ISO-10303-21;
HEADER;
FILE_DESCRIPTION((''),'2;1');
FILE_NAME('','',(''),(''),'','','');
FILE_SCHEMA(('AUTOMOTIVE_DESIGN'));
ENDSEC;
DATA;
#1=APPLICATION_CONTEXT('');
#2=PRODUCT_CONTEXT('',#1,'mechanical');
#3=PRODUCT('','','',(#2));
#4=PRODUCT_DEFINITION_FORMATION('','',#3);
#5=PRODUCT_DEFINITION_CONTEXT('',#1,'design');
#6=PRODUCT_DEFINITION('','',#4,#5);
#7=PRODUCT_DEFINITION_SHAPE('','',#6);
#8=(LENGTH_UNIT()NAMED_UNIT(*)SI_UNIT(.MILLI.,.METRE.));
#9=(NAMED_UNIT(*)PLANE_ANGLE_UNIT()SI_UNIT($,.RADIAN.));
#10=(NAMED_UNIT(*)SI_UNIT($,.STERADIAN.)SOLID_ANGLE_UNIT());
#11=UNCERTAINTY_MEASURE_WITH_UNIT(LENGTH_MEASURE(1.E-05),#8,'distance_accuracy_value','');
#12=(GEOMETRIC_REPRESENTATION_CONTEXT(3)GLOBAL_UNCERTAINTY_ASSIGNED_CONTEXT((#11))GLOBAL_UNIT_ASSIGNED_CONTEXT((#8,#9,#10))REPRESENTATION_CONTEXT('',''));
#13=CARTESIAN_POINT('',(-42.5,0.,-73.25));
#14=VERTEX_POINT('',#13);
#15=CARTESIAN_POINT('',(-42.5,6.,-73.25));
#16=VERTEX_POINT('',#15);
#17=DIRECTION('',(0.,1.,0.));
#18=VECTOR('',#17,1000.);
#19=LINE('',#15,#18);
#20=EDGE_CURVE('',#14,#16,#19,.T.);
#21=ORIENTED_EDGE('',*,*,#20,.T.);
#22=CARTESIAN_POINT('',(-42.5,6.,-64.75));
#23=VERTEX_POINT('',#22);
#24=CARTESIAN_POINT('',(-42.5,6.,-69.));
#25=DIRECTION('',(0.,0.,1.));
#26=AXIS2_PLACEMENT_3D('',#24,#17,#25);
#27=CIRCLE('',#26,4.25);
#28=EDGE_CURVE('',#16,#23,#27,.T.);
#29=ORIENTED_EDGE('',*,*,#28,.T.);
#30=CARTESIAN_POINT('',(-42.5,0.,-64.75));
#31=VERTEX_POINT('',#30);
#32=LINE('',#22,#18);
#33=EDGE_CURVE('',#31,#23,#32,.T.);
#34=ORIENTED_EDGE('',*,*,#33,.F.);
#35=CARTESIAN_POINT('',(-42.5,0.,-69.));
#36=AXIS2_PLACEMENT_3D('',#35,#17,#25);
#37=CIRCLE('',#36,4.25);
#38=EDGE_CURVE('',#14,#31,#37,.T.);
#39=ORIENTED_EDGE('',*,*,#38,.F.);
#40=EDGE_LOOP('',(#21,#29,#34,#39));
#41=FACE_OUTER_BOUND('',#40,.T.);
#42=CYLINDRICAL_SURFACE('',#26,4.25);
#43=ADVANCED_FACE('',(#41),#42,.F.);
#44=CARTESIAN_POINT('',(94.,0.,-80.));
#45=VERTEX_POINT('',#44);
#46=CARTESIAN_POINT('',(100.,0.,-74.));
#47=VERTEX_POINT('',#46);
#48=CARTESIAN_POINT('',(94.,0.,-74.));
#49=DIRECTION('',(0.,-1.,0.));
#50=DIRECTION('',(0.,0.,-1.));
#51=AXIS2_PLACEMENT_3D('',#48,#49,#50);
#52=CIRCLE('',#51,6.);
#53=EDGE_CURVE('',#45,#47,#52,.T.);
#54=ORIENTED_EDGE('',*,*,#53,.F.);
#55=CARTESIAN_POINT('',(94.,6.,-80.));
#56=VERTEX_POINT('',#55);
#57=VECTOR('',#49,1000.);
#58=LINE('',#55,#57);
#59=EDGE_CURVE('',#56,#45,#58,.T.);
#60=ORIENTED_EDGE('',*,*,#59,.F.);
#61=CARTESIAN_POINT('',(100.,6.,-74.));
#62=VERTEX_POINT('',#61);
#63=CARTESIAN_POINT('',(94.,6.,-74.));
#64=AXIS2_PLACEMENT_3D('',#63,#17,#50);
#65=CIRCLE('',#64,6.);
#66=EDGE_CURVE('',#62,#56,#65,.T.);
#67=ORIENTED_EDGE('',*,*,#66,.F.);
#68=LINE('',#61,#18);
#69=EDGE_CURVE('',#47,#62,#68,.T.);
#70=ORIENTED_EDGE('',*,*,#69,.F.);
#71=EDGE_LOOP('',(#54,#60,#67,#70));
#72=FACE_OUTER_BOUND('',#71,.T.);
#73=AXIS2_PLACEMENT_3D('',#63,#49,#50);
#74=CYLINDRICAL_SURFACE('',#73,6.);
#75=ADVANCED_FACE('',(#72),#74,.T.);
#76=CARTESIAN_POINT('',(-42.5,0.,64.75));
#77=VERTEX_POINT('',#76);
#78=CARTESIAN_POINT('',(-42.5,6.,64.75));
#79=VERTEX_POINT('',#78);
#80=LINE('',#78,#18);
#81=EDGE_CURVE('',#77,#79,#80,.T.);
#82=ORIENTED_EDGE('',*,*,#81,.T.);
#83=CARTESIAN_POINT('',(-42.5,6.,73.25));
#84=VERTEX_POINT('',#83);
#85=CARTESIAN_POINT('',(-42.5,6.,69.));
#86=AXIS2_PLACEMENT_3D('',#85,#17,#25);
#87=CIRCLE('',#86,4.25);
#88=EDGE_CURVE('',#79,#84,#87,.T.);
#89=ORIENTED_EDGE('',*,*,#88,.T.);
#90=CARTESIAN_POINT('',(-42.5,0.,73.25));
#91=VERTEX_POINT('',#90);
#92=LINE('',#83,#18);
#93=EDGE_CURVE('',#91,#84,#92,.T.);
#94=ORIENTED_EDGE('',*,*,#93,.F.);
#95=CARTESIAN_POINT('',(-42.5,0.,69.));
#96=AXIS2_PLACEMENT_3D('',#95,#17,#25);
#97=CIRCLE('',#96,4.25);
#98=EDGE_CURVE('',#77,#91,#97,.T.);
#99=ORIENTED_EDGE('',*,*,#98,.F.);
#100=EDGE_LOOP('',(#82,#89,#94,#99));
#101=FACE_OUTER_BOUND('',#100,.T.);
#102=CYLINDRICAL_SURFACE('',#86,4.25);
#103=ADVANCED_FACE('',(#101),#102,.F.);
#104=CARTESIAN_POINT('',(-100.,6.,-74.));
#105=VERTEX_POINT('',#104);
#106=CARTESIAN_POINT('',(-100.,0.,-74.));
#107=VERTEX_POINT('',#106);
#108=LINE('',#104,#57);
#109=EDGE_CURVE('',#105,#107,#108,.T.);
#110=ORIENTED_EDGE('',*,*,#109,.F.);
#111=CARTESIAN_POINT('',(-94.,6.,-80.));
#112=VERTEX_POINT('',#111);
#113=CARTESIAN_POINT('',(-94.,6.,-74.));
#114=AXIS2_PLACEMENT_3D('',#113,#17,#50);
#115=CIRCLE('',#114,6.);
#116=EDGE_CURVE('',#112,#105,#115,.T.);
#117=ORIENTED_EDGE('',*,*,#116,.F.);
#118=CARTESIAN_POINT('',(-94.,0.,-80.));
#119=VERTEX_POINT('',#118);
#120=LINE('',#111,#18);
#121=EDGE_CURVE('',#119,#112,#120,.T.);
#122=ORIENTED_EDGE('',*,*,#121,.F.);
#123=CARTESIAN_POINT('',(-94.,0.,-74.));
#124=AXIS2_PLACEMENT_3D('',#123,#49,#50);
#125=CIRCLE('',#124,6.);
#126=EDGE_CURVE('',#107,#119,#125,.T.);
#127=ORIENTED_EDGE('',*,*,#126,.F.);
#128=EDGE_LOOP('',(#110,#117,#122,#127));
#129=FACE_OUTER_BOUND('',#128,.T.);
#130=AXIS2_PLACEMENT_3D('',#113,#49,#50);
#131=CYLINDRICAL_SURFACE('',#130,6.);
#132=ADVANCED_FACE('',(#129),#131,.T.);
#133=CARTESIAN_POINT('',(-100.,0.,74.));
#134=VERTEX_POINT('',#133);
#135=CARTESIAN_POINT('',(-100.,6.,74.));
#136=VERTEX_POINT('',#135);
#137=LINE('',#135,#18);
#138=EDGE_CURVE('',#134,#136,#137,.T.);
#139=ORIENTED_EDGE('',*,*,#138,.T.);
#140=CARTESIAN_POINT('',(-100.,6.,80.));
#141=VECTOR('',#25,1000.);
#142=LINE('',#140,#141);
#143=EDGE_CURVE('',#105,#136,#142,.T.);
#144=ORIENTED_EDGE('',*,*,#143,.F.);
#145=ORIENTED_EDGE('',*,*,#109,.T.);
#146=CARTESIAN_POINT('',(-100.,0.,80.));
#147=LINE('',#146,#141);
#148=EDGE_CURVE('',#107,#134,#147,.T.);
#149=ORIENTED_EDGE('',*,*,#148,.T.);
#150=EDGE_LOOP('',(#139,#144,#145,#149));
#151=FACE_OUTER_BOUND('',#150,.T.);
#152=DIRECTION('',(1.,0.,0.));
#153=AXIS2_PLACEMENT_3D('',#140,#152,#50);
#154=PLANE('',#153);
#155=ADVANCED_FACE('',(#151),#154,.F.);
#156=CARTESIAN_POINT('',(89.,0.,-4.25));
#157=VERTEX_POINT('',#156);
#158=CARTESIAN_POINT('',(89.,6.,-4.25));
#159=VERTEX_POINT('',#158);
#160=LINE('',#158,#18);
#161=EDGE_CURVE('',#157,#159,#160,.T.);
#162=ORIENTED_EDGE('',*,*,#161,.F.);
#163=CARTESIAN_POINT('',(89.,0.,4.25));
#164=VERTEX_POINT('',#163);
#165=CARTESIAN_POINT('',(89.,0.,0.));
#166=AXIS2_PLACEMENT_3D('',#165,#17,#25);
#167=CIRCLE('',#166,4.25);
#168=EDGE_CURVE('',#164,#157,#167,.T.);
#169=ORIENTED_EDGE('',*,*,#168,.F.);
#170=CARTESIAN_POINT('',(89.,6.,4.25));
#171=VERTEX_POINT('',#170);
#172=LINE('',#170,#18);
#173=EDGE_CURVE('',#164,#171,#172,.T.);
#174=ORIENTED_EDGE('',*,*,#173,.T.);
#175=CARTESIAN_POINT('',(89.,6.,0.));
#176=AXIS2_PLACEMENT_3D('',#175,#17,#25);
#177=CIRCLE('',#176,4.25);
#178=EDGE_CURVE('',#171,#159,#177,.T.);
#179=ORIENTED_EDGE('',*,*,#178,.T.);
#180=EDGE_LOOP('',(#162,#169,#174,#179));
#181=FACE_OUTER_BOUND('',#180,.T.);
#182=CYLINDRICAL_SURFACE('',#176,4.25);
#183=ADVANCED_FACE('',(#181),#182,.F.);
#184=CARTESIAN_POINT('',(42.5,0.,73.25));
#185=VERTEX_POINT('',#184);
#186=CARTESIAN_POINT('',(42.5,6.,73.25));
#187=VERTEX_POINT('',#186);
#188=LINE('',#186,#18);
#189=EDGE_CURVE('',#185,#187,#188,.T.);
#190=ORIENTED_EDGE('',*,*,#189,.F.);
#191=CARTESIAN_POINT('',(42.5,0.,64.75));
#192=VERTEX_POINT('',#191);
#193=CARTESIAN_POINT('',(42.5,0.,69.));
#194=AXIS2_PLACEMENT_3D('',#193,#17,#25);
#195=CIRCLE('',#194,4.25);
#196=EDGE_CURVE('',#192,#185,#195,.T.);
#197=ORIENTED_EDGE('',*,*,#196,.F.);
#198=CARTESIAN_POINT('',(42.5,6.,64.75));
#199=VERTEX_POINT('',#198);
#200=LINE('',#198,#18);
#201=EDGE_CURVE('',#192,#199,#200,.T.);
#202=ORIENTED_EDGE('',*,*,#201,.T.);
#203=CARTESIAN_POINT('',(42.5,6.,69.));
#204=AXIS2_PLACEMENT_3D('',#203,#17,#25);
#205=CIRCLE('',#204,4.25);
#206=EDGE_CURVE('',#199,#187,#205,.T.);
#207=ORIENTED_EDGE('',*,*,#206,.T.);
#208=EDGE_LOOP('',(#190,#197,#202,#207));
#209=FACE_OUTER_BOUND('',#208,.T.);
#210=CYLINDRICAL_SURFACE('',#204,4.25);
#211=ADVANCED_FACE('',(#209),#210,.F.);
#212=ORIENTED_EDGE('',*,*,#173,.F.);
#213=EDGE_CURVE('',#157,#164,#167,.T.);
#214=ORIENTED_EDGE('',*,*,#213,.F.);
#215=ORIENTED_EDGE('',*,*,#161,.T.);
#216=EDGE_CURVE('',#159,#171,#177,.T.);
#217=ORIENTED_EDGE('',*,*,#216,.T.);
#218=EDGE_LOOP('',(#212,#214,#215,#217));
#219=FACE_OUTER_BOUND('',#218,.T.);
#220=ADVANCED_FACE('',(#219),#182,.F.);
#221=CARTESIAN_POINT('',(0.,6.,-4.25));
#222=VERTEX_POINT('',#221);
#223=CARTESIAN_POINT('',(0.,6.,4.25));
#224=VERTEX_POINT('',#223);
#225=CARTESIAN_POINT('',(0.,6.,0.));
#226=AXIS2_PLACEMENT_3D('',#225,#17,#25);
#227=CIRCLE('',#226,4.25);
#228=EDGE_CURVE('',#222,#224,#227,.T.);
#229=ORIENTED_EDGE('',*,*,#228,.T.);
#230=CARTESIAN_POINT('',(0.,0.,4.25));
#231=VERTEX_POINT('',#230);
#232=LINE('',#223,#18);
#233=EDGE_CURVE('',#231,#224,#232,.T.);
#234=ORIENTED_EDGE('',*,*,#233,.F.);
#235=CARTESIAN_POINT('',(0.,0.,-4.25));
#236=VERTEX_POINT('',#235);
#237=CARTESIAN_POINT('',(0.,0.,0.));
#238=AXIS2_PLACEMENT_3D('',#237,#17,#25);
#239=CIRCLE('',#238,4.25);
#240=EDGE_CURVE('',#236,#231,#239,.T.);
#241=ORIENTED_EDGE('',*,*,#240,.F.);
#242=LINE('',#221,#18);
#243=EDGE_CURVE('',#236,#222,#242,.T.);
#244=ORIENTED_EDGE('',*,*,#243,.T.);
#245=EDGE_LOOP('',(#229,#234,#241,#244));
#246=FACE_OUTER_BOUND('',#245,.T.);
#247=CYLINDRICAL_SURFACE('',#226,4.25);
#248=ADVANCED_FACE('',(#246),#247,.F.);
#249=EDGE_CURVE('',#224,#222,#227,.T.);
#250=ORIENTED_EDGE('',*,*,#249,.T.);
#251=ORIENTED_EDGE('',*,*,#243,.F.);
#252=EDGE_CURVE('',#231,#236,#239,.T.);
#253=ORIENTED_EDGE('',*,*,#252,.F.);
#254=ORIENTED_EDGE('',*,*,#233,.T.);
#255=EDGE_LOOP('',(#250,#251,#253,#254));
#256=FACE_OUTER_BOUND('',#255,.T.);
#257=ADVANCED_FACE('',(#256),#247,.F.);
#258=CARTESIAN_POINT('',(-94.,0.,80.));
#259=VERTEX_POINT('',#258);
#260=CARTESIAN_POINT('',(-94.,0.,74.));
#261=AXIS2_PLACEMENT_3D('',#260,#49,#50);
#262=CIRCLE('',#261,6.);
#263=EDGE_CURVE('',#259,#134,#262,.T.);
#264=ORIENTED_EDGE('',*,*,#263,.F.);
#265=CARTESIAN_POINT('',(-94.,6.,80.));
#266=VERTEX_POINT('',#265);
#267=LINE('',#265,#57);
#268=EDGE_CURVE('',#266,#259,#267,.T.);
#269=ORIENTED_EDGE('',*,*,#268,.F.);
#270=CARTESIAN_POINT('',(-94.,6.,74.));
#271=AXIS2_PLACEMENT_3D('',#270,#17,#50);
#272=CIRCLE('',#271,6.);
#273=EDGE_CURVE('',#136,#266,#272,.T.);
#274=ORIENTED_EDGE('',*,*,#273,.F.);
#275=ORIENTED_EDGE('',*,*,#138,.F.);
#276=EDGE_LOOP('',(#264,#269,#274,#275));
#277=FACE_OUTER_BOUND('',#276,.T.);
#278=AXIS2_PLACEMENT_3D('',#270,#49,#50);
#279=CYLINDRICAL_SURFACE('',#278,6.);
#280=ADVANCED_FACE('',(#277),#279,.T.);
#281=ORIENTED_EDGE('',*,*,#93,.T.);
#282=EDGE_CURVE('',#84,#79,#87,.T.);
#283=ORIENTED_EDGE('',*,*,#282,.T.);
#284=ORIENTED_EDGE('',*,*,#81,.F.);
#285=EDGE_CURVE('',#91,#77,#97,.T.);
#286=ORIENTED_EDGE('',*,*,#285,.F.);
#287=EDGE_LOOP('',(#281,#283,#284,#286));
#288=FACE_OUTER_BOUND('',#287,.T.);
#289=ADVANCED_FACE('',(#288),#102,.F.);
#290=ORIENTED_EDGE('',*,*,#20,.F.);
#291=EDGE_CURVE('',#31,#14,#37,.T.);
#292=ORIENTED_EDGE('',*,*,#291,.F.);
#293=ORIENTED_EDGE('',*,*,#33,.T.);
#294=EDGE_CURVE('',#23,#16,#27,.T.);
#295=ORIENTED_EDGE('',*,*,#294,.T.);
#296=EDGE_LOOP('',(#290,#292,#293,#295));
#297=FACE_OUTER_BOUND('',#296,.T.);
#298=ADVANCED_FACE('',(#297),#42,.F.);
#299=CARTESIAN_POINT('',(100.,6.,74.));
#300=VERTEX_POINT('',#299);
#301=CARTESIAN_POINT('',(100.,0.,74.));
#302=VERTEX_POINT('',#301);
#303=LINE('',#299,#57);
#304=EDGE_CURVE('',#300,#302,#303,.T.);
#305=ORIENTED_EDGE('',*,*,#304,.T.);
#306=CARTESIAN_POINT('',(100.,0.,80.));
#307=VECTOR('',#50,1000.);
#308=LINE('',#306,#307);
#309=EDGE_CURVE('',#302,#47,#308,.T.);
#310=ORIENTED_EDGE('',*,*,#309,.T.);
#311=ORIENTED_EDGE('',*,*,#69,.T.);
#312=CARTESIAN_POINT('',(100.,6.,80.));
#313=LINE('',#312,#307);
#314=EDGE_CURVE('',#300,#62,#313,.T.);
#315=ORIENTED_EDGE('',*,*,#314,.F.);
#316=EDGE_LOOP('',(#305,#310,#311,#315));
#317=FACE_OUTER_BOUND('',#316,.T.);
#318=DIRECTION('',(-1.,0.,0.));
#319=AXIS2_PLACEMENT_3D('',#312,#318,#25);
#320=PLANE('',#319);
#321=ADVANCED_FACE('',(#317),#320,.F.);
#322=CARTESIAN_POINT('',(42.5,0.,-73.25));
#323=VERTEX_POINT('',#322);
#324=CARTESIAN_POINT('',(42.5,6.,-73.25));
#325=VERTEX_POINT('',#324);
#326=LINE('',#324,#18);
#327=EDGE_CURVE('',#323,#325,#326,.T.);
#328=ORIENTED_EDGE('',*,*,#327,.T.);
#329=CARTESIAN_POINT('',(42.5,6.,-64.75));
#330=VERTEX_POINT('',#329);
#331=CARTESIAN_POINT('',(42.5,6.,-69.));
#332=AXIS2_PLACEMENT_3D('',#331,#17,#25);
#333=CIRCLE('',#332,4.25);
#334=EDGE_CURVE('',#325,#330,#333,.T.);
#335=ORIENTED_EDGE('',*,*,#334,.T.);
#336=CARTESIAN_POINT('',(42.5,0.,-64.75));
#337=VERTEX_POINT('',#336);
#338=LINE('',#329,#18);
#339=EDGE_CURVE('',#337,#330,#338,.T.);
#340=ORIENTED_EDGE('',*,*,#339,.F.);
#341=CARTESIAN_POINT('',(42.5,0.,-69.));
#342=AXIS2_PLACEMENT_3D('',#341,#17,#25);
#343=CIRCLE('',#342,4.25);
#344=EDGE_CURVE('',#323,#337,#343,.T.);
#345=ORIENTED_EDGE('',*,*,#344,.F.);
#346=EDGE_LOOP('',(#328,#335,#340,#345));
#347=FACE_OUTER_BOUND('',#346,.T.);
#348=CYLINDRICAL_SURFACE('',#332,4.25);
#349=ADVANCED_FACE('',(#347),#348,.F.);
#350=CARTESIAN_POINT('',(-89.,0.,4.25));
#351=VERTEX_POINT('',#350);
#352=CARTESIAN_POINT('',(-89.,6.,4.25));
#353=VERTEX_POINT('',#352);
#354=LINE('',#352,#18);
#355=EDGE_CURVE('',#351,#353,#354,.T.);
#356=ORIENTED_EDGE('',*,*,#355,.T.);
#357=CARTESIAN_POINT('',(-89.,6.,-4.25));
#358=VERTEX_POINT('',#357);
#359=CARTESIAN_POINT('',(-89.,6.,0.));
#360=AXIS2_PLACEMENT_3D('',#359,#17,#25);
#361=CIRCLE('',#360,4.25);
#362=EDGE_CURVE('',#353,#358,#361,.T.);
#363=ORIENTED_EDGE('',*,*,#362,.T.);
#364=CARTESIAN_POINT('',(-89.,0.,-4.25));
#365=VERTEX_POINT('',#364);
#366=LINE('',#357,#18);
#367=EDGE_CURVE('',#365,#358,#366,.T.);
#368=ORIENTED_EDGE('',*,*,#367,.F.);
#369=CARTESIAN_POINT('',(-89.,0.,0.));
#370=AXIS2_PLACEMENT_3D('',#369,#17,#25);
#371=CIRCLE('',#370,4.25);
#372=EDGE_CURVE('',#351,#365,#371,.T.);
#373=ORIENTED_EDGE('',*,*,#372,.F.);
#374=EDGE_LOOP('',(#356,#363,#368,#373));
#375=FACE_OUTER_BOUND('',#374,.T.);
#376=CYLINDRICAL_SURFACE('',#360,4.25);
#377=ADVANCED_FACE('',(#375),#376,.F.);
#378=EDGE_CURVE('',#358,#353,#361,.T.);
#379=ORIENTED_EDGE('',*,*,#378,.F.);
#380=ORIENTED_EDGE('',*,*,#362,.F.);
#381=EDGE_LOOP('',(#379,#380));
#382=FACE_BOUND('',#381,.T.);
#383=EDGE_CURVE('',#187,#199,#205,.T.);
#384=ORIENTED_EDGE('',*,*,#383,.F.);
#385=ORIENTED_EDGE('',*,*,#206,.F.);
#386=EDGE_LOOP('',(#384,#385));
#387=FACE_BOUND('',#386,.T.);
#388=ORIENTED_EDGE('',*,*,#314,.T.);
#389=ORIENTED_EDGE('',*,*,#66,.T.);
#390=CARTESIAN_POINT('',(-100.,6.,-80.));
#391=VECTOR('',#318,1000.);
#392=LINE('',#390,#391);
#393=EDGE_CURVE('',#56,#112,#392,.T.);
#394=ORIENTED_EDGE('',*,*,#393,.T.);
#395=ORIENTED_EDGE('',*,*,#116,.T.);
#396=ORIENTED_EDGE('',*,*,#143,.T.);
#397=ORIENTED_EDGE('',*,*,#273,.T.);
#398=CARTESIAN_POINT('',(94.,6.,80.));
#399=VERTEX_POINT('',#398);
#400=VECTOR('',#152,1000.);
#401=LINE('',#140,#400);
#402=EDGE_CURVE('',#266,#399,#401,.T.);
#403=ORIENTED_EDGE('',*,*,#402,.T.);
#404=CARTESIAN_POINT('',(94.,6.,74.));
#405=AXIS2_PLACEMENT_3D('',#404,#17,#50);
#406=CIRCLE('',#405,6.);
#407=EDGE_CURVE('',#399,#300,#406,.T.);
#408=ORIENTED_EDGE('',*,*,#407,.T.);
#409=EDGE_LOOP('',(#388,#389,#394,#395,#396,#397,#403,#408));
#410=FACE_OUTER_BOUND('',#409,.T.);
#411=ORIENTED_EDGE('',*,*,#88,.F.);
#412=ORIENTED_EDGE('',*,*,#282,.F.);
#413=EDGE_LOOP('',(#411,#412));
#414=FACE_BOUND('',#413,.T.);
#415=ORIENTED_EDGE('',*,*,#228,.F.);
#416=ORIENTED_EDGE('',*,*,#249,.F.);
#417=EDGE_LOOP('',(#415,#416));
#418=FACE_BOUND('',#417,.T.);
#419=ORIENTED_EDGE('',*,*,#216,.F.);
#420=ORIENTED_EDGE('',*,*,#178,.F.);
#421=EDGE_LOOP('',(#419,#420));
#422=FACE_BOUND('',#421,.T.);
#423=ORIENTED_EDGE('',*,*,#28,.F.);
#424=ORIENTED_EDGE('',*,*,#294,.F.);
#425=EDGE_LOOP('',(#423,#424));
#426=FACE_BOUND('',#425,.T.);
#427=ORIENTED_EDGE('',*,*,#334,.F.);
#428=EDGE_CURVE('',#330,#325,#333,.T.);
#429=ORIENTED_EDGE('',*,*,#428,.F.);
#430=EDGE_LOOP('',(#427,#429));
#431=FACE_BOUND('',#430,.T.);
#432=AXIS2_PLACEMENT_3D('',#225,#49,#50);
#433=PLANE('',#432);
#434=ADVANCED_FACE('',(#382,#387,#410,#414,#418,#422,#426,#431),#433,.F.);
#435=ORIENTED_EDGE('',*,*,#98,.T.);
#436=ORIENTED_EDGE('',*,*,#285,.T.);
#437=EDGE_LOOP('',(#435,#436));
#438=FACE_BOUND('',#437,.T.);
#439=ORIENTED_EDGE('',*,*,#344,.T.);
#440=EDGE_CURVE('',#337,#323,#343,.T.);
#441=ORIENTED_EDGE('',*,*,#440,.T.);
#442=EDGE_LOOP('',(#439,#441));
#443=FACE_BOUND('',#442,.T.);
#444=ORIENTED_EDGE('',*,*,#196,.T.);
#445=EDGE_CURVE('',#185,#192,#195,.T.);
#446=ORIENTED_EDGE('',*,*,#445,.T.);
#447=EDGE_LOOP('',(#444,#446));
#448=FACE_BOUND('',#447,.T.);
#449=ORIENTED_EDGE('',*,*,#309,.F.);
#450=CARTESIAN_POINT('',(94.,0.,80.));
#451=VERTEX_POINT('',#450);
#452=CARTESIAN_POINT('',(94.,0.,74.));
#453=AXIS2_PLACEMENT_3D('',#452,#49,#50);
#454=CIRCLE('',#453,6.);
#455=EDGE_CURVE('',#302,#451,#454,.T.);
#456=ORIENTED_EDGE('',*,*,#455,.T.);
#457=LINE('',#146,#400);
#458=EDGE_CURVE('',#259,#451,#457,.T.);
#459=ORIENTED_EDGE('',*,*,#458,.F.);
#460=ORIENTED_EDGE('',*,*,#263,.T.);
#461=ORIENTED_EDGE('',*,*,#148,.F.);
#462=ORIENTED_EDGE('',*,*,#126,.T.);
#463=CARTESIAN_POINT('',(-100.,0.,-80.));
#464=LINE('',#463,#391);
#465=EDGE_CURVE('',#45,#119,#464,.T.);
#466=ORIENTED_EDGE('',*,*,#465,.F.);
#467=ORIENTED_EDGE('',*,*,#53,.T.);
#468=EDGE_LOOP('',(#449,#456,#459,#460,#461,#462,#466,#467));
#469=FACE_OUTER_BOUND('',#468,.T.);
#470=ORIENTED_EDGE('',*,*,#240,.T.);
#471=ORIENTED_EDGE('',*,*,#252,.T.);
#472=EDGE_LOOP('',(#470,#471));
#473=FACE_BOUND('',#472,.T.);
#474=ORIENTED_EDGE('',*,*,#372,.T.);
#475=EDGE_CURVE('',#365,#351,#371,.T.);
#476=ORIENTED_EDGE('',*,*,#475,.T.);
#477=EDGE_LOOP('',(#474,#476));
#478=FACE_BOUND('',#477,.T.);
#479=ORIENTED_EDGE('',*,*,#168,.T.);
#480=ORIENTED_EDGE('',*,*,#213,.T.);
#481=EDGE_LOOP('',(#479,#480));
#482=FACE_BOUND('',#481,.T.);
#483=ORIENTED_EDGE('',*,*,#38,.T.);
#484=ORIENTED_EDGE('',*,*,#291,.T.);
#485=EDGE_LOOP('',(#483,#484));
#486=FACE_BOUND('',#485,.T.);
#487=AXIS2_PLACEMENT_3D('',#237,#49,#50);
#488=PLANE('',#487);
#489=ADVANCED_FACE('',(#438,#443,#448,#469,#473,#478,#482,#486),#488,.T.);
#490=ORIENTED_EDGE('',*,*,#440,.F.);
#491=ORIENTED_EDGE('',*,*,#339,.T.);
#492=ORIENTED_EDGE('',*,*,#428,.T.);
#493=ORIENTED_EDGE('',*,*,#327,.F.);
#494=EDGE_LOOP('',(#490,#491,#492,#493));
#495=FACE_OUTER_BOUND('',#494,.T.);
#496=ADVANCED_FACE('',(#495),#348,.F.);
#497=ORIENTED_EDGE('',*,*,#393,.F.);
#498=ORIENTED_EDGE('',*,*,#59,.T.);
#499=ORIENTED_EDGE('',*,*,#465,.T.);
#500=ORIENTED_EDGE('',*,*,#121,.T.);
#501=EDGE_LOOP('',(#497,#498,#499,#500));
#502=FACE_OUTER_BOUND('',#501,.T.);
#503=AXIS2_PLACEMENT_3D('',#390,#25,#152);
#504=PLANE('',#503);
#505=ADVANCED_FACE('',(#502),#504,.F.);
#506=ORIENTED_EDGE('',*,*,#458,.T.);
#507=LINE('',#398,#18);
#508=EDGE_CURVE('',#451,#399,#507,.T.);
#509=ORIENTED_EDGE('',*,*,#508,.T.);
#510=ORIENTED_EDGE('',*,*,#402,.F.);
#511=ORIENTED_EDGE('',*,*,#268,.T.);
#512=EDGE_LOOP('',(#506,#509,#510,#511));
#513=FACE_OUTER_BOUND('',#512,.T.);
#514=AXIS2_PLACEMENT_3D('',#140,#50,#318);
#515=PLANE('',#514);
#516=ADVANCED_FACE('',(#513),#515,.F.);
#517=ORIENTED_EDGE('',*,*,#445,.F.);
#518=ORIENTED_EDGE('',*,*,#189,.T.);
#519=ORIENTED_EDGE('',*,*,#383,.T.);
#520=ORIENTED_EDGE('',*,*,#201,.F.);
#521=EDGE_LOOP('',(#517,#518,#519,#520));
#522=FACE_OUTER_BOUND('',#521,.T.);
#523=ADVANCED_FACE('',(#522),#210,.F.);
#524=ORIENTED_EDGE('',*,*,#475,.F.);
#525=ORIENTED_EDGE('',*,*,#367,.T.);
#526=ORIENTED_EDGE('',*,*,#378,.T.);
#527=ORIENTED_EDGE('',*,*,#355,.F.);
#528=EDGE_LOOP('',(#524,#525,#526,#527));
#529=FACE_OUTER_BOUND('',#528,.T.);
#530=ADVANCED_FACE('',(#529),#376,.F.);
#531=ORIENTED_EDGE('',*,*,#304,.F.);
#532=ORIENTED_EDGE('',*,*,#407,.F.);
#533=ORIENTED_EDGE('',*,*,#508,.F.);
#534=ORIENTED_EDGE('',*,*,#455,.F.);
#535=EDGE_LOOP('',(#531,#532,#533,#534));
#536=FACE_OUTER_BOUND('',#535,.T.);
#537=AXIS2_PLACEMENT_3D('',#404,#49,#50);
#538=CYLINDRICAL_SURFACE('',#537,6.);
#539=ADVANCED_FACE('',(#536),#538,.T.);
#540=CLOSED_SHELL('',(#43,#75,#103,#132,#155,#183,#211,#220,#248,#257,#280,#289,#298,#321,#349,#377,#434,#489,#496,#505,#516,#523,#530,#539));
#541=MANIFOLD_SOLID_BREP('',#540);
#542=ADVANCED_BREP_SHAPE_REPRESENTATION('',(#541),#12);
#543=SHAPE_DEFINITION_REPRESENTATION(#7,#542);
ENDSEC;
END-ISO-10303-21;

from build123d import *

# Parameters (mm, degrees)
SKETCH1_W           = 200
SKETCH1_H           = 160
BOSS_EXTRUDE1_DEPTH = 6
FILLET1_R           = 6
M10_TAPPED_HOLE1_D  = 8.5


with BuildPart() as part:
    # Sketch1 → Boss-Extrude1 (new body)
    with BuildSketch(Plane(origin=(0, 0, 0), x_dir=(1, 0, 0), z_dir=(0, 1, 0))):
        Rectangle(SKETCH1_W, SKETCH1_H)
    extrude(amount=BOSS_EXTRUDE1_DEPTH)

    # Fillet1
    fillet1_edges = [part.edges().sort_by_distance(p)[0] for p in [
        (100, 3, 80),
        (-100, 3, 80),
        (-100, 3, -80),
        (100, 3, -80),
    ]]
    fillet(fillet1_edges, radius=FILLET1_R)

    # M10 Tapped Hole1 (through all)
    with Locations(Plane(origin=(0, 6, 0), x_dir=(1, 0, 0), z_dir=(0, 1, 0))):
        with Locations((0, 0), (42.5, 69), (-42.5, 69), (-89, 0), (89, 0), (42.5, -69), (-42.5, -69)):
            Hole(M10_TAPPED_HOLE1_D / 2)


solid = part.part
